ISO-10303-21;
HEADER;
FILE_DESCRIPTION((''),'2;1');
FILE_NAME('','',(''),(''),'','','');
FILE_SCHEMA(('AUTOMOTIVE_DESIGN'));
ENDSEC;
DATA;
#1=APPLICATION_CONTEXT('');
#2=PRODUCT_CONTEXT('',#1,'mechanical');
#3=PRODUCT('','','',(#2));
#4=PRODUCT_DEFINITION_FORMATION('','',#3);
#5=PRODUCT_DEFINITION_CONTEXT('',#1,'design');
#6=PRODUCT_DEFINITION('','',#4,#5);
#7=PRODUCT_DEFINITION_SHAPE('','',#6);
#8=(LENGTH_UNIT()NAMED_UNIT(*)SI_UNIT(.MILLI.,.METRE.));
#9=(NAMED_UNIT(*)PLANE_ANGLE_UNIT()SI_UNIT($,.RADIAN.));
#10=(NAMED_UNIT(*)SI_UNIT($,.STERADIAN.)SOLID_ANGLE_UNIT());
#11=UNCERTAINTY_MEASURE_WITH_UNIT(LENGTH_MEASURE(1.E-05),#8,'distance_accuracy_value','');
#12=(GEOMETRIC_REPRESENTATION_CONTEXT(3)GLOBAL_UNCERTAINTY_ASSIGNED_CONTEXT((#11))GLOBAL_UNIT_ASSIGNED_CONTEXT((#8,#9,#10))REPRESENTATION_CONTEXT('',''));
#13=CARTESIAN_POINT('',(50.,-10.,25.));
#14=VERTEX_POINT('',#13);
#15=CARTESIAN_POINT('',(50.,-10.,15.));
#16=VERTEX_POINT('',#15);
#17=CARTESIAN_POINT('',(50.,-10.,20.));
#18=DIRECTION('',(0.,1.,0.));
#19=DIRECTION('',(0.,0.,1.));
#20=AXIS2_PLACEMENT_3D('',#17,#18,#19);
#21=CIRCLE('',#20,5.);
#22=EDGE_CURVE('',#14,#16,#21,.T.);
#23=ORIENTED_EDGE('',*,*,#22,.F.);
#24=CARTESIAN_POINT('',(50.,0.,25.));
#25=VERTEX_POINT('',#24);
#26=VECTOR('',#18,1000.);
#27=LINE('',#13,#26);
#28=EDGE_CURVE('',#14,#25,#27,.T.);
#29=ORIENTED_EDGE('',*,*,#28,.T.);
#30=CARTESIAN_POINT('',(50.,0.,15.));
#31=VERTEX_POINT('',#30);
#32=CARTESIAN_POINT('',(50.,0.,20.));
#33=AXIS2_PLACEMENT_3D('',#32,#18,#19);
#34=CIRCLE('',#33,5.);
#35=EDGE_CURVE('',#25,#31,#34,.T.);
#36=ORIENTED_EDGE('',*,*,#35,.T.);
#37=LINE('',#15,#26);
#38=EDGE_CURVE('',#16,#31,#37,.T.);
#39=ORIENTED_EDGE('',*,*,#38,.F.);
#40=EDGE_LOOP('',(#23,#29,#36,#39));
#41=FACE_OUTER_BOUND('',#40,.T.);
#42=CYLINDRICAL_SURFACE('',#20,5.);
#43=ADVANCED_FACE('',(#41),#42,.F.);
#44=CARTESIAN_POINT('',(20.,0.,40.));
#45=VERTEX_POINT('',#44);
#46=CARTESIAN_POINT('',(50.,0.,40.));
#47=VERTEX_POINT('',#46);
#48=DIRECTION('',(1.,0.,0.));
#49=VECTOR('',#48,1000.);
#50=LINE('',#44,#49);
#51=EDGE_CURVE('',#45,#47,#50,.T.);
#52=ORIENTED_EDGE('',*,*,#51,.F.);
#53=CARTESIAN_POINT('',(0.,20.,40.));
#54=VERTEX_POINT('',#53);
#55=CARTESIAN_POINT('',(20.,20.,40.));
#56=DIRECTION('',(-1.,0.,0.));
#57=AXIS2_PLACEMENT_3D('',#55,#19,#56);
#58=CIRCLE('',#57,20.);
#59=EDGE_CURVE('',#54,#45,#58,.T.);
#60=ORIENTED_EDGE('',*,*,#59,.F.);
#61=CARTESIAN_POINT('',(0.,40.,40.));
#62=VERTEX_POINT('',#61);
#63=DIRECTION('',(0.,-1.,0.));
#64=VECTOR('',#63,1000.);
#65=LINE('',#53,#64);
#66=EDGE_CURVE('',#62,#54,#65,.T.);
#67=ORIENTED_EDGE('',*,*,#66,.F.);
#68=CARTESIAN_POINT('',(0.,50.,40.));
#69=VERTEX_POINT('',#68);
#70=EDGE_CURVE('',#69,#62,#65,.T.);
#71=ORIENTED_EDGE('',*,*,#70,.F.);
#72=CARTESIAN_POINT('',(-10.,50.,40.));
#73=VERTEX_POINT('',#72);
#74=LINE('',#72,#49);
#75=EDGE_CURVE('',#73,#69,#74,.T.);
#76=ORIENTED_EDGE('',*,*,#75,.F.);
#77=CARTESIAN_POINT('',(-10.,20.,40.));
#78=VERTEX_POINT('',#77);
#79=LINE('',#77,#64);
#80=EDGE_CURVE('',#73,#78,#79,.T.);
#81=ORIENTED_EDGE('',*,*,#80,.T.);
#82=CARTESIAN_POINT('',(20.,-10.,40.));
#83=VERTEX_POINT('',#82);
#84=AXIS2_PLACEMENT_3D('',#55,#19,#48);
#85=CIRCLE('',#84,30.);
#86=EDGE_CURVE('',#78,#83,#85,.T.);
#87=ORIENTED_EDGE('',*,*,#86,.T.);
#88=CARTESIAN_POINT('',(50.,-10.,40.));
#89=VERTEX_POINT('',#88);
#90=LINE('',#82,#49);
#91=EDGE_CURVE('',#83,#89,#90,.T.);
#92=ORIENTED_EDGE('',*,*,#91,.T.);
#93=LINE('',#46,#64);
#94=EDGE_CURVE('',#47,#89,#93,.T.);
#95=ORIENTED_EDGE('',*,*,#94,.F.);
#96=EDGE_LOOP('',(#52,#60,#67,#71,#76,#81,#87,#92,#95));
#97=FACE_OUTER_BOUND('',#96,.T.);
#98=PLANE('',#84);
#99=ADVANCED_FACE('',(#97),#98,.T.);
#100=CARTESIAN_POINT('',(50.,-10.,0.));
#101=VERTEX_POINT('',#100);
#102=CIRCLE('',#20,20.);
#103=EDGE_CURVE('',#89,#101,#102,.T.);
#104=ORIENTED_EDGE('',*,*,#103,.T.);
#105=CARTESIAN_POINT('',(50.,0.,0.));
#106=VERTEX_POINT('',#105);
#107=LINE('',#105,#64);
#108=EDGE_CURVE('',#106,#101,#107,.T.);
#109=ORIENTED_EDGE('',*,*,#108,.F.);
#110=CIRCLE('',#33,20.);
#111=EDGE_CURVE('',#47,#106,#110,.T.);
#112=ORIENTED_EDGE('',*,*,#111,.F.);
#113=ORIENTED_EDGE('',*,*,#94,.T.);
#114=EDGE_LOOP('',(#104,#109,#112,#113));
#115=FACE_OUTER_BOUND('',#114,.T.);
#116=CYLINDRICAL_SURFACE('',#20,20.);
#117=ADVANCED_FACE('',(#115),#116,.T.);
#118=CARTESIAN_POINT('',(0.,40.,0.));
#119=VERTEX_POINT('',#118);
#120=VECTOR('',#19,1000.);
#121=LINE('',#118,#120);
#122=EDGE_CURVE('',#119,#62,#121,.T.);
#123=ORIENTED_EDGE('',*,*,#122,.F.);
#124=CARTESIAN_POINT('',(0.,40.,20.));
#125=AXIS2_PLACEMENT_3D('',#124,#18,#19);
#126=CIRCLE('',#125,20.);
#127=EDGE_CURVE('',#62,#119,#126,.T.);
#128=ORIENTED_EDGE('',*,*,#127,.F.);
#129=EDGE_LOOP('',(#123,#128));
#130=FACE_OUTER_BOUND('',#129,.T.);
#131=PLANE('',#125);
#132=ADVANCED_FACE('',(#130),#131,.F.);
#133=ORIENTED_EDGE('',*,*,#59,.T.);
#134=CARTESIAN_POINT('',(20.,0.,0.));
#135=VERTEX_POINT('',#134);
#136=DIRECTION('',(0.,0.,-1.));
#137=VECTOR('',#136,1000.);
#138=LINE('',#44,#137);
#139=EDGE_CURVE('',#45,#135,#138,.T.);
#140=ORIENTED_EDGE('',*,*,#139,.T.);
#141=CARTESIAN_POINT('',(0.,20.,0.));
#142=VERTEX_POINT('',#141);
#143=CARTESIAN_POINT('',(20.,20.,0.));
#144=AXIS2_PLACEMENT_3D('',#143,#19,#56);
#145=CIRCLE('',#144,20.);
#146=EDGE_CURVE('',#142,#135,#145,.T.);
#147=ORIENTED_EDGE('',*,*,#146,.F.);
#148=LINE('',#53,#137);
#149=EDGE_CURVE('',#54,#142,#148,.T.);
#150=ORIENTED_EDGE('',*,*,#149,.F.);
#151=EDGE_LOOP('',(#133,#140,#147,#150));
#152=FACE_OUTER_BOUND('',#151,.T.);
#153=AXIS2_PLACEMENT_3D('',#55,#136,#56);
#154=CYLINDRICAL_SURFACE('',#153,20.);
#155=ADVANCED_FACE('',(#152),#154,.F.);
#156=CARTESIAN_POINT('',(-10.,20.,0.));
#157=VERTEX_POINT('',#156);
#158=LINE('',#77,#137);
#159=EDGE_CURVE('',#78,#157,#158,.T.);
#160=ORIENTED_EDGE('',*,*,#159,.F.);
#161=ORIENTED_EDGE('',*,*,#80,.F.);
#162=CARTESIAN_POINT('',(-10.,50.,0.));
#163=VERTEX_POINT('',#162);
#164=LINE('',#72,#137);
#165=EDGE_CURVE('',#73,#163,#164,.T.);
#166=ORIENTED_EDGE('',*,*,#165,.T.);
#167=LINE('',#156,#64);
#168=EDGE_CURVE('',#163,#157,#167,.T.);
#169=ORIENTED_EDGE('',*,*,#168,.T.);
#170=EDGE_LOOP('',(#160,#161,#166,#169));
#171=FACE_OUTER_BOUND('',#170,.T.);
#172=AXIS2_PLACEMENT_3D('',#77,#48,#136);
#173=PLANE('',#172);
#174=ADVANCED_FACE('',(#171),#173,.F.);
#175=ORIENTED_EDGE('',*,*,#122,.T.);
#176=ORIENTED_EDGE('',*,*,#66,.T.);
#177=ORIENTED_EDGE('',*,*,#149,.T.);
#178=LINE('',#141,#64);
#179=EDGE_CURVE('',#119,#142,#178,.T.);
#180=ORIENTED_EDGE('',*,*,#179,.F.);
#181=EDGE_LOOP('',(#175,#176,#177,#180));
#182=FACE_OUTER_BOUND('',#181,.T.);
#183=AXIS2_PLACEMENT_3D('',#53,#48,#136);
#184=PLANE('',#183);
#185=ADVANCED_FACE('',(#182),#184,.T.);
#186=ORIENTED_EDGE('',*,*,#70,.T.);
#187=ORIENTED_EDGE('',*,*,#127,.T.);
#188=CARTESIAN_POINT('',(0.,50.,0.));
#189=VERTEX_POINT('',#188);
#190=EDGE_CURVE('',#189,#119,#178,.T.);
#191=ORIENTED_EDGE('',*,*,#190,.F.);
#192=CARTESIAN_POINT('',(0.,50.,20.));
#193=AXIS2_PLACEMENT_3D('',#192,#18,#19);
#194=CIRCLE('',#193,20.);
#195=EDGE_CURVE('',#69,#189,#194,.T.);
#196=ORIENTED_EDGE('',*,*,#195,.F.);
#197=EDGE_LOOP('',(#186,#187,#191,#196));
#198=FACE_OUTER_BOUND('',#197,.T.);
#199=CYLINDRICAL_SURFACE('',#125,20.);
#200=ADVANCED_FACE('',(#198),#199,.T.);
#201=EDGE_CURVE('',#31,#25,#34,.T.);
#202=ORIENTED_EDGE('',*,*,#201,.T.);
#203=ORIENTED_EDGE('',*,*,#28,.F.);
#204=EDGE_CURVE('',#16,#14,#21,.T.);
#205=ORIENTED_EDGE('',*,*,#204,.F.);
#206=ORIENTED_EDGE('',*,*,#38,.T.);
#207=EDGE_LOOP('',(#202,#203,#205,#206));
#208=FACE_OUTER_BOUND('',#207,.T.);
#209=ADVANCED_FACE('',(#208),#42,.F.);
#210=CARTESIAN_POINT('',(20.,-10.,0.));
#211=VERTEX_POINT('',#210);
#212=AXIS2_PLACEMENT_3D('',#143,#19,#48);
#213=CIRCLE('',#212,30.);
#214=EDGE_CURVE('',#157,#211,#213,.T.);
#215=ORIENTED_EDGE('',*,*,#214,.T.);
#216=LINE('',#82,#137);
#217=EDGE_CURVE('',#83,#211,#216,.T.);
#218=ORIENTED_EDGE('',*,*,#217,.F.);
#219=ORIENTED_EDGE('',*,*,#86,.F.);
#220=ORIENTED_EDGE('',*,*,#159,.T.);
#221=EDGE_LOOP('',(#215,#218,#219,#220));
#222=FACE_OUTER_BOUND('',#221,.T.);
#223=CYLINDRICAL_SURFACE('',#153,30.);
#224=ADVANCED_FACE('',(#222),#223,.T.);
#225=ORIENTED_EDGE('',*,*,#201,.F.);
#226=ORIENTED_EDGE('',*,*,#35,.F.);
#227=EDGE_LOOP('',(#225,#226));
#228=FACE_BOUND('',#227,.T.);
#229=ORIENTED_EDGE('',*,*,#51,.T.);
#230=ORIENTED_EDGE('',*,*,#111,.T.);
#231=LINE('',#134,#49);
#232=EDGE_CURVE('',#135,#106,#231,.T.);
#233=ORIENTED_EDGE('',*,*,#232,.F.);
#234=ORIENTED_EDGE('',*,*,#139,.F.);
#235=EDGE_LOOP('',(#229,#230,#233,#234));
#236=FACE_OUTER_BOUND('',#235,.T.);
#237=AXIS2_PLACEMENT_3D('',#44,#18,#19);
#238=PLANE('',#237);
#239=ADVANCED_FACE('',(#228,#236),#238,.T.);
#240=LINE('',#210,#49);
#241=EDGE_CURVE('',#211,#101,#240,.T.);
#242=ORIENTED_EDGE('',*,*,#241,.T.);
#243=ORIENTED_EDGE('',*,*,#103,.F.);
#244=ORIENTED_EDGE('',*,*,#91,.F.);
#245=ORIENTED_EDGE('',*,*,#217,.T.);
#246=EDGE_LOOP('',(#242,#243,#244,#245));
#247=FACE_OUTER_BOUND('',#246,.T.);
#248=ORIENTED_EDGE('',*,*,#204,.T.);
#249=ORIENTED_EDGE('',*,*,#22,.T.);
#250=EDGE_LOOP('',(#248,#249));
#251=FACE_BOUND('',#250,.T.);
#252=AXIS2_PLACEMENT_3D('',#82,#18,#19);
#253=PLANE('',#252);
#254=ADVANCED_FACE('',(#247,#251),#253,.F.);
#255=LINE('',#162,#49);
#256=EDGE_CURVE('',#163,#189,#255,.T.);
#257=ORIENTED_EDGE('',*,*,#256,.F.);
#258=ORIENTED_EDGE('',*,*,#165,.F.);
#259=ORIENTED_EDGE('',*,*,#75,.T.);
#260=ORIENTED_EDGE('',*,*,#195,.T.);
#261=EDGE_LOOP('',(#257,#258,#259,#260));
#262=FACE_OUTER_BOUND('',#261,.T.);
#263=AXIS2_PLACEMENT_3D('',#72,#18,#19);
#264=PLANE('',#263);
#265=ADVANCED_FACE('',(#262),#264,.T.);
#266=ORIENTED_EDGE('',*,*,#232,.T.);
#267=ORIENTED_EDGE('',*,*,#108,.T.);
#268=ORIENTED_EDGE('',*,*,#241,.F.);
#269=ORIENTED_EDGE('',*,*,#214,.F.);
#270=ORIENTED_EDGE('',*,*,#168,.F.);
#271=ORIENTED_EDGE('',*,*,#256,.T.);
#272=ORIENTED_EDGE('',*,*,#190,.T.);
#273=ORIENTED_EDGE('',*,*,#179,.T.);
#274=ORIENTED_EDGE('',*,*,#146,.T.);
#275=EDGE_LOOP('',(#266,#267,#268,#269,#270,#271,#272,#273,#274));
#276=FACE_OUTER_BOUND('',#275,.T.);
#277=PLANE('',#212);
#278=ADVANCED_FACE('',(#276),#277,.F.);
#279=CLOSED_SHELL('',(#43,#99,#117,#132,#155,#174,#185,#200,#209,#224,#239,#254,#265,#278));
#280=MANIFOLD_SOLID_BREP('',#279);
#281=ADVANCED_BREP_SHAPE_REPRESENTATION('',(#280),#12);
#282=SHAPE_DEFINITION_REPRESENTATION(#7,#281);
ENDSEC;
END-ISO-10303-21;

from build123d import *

# Parameters (mm, degrees)
CURVED_BRACKET_WALL_DEPTH = 40
ROUNDED_END_TAB_DEPTH     = 10
MOUNTING_TAB_DEPTH        = 10
MOUNTING_HOLE_SKETCH_R    = 5
MOUNTING_HOLE_10_DEPTH    = 10


with BuildPart() as part:
    # Bracket Profile Sketch → Curved Bracket Wall (new body)
    with BuildSketch(Plane.XY):
        with BuildLine():
            Line((50, 0), (20, 0))
            ThreePointArc((20, 0), (5.857864376, 5.857864376), (0, 20))
            Line((0, 20), (0, 50))
            Line((0, 50), (-10, 50))
            Line((-10, 50), (-10, 20))
            ThreePointArc((-10, 20), (-1.213203436, -1.213203436), (20, -10))
            Line((20, -10), (50, -10))
            Line((50, -10), (50, 0))
        make_face()
    extrude(amount=CURVED_BRACKET_WALL_DEPTH)

    # Rounded Tab Sketch → Rounded End Tab (add)
    with BuildSketch(Plane(origin=(0, 50, 0), x_dir=(1, 0, 0), z_dir=(0, 1, 0))):
        with BuildLine():
            Line((0, 0), (0, -40))
            ThreePointArc((0, -40), (20, -20), (0, 0))
        make_face()
    extrude(amount=-ROUNDED_END_TAB_DEPTH)

    # Mounting Tab Sketch → Mounting Tab (add)
    with BuildSketch(Plane(origin=(0, 0, 0), x_dir=(1, 0, 0), z_dir=(0, 1, 0))):
        with BuildLine():
            Line((50, 0), (50, -40))
            ThreePointArc((50, -40), (70, -20), (50, 0))
        make_face()
    extrude(amount=-MOUNTING_TAB_DEPTH)

    # Mounting Hole Sketch → Mounting Hole Ø10 (cut)
    with BuildSketch(Plane(origin=(0, 0, 0), x_dir=(1, 0, 0), z_dir=(0, 1, 0))):
        with Locations(Location((50, -20, 0), (0, 0, 270))):
            Circle(MOUNTING_HOLE_SKETCH_R)
    extrude(amount=-MOUNTING_HOLE_10_DEPTH, mode=Mode.SUBTRACT)


solid = part.part
